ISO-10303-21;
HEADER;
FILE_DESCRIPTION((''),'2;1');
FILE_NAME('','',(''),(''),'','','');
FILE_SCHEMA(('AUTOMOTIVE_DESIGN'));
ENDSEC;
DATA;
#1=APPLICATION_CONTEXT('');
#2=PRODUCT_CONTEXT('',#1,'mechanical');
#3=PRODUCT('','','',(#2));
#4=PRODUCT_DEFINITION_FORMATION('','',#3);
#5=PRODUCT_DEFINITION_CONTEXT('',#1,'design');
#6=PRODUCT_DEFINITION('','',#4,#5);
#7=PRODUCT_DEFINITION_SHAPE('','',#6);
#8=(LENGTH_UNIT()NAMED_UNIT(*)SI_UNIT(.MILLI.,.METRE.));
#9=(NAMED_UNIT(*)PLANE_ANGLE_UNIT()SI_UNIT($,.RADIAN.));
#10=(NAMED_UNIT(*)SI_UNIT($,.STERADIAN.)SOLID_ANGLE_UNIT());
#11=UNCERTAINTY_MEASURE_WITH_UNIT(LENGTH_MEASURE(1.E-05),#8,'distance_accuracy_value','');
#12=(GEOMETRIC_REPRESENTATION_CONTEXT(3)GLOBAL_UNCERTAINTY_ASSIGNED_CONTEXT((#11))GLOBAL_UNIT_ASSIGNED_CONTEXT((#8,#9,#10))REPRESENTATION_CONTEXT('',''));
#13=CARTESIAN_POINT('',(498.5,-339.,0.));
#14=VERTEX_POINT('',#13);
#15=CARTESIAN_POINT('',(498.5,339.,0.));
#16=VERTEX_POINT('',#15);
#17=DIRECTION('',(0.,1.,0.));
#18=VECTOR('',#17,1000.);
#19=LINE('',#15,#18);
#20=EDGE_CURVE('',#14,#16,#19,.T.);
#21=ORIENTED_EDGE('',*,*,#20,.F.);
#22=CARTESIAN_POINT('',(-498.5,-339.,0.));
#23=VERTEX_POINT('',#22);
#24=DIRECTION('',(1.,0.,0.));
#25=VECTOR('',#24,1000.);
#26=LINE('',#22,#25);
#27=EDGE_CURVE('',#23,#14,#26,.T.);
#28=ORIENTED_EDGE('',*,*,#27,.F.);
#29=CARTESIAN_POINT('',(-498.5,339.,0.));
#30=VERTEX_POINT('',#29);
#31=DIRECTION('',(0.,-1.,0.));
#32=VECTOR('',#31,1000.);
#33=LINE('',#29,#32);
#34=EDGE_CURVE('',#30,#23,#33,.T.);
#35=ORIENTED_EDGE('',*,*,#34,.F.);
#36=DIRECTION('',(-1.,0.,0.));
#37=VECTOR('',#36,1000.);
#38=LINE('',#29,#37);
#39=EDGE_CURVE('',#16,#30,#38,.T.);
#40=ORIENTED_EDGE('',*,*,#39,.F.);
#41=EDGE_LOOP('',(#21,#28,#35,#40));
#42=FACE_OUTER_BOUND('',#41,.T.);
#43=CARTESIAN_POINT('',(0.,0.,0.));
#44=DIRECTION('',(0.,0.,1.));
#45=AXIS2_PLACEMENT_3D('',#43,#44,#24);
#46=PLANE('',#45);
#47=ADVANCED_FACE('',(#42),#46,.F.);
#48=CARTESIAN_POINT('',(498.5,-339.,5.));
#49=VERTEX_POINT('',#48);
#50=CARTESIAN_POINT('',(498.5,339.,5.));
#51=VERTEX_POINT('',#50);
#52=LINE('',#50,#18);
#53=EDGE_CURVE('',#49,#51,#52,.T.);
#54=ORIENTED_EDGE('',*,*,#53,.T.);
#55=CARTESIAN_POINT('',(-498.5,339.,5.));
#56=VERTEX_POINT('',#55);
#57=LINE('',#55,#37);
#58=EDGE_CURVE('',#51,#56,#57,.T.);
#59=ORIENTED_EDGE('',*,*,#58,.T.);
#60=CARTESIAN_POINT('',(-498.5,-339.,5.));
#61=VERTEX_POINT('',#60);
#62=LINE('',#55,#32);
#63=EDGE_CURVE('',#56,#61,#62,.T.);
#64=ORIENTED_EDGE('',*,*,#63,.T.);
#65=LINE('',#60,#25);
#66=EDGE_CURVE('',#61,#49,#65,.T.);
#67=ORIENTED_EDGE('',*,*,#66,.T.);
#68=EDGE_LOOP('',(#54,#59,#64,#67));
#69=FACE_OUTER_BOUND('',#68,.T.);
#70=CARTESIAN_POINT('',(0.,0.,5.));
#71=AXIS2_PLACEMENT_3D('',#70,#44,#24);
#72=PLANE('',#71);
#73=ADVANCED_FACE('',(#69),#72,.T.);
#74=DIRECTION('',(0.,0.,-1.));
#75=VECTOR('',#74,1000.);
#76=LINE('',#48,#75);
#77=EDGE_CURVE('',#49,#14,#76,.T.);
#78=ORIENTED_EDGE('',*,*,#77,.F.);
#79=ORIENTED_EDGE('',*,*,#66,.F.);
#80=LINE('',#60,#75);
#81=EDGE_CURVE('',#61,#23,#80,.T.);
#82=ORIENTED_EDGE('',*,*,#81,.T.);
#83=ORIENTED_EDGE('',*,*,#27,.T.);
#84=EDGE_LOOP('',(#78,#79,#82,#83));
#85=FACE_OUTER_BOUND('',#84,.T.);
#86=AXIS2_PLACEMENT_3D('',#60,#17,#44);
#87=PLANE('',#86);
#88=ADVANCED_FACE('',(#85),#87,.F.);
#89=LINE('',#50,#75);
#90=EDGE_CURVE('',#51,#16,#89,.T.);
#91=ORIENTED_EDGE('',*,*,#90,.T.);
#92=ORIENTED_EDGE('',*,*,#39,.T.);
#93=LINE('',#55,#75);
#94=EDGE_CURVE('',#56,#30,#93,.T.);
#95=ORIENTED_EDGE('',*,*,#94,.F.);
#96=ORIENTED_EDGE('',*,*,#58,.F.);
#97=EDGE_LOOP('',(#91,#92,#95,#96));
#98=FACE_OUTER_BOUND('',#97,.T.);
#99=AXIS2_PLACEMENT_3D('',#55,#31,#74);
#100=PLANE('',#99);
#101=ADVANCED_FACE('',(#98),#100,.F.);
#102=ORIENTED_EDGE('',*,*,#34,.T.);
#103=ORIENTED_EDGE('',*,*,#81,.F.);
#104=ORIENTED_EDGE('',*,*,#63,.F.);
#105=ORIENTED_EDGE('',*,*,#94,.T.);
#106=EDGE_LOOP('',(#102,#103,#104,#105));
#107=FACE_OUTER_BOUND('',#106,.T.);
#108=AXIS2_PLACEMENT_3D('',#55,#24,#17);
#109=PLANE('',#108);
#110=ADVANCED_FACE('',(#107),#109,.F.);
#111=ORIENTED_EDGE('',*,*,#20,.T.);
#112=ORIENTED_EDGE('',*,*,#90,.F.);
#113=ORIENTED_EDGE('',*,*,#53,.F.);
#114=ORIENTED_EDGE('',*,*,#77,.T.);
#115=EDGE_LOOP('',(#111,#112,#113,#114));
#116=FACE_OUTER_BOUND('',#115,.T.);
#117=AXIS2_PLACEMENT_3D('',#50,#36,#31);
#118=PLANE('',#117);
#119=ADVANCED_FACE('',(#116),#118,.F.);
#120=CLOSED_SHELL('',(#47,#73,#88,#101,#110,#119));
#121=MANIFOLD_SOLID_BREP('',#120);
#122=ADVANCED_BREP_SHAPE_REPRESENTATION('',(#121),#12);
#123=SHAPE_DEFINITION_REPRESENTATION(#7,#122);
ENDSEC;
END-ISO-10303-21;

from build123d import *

# Parameters (mm, degrees)
SKETCH_1_W      = 997
SKETCH_1_H      = 678
EXTRUDE_1_DEPTH = 5


with BuildPart() as part:
    # 草图1 → 凸台-拉伸1 (new body)
    with BuildSketch(Plane.XY):
        Rectangle(SKETCH_1_W, SKETCH_1_H)
    extrude(amount=EXTRUDE_1_DEPTH)


solid = part.part
